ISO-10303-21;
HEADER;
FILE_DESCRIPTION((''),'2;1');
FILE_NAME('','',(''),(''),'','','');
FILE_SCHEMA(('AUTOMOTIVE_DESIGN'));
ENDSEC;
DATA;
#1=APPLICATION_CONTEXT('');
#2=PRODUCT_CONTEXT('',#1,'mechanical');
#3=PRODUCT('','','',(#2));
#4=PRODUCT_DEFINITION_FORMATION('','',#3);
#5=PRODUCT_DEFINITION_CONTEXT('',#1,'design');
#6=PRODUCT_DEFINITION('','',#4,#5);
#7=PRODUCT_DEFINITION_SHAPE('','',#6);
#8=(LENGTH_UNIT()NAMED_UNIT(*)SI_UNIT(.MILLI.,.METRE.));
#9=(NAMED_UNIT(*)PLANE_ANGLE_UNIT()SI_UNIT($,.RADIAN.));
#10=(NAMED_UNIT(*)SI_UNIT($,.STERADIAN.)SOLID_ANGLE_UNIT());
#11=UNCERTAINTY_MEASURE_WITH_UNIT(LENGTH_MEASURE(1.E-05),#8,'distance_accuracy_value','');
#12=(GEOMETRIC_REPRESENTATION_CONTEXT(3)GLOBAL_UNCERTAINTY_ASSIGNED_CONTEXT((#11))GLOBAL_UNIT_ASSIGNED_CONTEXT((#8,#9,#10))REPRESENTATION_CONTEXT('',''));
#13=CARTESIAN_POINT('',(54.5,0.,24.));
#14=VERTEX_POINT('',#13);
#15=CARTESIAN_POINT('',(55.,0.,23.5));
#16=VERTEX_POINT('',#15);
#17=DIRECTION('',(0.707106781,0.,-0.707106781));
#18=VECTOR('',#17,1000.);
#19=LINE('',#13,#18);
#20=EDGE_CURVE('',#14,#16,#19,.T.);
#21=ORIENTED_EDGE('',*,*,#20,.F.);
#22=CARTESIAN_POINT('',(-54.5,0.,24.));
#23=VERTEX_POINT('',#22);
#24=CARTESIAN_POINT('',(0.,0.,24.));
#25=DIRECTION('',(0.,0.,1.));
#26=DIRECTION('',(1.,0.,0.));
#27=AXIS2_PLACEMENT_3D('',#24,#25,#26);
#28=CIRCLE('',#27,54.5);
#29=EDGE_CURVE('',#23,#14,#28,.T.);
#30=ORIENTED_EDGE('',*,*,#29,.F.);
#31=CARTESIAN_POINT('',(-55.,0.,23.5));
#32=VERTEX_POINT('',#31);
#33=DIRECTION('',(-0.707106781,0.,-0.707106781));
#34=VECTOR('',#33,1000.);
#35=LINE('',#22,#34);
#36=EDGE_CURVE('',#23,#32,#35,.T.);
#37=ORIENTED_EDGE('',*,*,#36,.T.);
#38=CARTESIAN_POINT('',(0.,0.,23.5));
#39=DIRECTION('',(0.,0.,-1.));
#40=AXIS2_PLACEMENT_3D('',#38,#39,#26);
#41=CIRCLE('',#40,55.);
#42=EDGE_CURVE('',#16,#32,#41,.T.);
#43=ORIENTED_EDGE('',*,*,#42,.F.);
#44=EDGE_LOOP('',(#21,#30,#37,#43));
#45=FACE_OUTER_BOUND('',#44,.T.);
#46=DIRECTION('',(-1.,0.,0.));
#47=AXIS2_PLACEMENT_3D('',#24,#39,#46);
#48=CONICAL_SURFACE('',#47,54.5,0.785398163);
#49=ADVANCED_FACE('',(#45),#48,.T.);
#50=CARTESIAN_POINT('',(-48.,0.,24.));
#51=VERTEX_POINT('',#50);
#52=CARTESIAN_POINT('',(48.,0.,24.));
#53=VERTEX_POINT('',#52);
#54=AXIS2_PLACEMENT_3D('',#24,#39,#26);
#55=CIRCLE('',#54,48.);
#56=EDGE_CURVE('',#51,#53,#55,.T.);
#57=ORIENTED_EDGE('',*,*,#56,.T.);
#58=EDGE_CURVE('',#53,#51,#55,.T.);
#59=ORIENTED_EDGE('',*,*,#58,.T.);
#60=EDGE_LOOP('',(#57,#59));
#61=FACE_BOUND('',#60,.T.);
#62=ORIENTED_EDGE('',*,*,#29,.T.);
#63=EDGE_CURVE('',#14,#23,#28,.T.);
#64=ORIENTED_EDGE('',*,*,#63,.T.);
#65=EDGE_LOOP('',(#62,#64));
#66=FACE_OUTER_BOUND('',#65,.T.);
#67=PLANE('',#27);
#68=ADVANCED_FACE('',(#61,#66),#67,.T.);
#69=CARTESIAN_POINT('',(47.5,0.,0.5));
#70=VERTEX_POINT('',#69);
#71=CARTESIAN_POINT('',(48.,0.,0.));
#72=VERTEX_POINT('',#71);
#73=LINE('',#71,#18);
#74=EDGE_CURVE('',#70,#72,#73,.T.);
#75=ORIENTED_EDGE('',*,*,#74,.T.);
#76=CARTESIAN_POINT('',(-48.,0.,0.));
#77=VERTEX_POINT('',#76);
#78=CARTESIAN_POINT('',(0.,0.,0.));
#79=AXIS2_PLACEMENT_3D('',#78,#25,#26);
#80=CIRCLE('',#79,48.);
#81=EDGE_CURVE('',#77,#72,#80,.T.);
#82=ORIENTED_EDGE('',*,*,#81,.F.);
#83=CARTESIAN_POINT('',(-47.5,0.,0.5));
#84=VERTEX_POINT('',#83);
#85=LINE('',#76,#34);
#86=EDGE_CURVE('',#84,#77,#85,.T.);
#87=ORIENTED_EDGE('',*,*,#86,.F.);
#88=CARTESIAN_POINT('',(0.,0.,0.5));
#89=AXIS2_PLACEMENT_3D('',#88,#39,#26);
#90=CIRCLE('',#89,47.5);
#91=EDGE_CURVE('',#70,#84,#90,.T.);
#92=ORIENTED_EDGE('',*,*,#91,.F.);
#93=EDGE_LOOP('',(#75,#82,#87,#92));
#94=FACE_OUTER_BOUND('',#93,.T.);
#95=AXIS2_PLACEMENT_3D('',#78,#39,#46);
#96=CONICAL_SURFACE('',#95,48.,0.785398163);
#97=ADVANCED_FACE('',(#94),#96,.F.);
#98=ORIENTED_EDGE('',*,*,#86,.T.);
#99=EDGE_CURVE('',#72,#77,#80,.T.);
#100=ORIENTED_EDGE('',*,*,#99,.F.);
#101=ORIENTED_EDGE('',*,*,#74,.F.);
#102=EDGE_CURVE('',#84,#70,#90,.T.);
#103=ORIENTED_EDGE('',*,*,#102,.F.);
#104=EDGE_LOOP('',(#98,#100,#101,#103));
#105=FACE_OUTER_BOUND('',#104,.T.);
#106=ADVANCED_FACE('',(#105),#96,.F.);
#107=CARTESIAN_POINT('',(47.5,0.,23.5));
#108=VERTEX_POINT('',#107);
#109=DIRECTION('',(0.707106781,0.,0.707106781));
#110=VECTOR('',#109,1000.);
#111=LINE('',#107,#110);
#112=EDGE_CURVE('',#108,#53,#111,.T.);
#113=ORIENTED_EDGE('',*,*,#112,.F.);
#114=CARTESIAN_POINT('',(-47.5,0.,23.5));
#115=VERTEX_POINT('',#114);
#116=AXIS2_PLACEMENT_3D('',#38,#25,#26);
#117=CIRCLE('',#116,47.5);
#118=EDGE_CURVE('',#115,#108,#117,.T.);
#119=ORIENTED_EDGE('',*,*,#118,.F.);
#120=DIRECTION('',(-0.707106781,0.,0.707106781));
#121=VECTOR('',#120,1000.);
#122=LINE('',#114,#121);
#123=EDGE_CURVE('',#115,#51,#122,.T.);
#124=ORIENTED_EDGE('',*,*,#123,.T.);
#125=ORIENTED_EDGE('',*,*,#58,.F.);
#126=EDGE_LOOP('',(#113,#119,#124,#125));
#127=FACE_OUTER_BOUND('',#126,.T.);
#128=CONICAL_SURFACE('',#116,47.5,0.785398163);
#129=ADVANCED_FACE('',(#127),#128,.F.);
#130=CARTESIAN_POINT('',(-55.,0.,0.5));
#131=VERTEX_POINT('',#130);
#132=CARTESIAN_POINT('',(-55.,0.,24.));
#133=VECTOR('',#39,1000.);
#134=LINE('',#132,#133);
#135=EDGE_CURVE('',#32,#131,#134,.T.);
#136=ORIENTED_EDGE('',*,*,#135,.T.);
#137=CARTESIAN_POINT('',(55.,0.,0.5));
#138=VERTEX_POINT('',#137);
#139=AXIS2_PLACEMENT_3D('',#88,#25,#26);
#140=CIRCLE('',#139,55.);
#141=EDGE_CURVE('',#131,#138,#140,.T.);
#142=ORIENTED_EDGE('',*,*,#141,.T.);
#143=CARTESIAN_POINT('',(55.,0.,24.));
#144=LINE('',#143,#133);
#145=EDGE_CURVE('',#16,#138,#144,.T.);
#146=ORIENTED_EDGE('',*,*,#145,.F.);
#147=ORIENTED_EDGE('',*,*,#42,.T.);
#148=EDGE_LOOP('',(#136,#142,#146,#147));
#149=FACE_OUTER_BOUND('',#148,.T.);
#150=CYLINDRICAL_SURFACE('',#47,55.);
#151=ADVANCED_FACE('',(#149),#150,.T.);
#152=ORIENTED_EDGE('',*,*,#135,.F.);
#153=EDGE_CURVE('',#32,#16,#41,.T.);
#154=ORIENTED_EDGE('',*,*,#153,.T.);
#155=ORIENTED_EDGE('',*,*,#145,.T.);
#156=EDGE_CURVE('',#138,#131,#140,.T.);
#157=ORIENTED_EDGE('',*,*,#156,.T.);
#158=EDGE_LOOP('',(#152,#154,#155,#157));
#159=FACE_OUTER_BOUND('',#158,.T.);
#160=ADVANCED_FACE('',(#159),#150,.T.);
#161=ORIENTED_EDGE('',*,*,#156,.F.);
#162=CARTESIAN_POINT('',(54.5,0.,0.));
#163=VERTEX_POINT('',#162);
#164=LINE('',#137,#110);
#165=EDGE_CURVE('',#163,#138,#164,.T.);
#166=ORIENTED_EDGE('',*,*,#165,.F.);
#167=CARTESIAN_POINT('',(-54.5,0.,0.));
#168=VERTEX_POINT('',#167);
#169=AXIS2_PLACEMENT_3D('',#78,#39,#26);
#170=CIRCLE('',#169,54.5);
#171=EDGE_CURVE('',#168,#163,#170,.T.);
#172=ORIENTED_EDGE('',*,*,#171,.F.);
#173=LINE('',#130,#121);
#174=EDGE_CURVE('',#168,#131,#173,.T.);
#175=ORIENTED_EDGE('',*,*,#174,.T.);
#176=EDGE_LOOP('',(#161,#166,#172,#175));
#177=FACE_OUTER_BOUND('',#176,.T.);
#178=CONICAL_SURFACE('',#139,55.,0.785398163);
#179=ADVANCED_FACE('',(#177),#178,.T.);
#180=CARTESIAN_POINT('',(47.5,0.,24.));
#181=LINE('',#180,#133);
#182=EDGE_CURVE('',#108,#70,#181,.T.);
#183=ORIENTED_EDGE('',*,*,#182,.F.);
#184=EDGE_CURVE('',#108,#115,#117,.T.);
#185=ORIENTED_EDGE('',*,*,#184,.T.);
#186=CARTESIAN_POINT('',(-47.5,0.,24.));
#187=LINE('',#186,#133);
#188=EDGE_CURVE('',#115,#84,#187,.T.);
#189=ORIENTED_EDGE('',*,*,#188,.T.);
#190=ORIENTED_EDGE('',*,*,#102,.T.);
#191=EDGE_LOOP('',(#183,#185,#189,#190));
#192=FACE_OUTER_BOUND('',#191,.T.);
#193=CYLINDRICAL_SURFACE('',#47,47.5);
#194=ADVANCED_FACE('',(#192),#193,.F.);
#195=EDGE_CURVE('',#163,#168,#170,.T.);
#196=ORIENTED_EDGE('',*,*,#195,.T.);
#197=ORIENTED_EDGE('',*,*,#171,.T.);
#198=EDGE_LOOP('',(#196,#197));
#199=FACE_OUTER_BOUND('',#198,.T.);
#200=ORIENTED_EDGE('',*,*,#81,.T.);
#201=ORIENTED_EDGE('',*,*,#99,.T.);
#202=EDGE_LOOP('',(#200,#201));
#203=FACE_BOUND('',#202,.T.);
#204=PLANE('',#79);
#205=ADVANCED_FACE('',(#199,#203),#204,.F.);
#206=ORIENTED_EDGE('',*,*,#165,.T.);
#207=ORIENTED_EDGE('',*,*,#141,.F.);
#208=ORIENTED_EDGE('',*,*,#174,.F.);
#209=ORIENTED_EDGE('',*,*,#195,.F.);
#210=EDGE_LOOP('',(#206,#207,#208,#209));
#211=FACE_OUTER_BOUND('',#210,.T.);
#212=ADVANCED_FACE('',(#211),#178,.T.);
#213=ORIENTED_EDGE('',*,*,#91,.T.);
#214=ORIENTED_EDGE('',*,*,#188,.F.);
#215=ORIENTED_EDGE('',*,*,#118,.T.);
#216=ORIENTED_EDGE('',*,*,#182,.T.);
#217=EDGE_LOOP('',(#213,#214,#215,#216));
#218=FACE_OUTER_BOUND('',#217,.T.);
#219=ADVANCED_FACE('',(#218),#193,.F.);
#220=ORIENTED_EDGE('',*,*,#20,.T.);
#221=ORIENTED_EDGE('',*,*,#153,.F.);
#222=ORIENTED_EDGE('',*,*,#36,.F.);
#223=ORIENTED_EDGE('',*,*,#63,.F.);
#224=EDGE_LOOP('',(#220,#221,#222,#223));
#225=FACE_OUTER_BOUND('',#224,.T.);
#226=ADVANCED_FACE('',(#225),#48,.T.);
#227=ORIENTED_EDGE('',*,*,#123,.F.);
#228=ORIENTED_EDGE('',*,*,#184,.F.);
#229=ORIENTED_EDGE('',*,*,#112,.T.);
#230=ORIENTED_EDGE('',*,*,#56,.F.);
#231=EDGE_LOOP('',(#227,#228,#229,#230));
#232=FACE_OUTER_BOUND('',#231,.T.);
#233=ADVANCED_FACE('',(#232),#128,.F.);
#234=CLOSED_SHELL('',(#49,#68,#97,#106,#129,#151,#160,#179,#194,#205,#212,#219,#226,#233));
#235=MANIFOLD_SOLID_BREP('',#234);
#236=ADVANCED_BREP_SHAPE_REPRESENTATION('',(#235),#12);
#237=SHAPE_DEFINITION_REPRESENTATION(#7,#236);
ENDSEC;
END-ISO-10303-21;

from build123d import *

# Parameters (mm, degrees)
SKETCH1_R           = 55
SKETCH1_R_2         = 47.5
BOSS_EXTRUDE1_DEPTH = 24
CHAMFER1_SIZE       = 0.5


with BuildPart() as part:
    # Sketch1 → Boss-Extrude1 (new body)
    with BuildSketch(Plane.XY):
        Circle(SKETCH1_R)
        Circle(SKETCH1_R_2, mode=Mode.SUBTRACT)
    extrude(amount=BOSS_EXTRUDE1_DEPTH)

    # Chamfer1
    chamfer1_edges = [part.edges().sort_by_distance(p)[0] for p in [
        (-55, 0, 0),
        (-55, 0, 24),
        (-47.5, 0, 0),
        (-47.5, 0, 24),
    ]]
    chamfer(chamfer1_edges, length=CHAMFER1_SIZE)


solid = part.part
